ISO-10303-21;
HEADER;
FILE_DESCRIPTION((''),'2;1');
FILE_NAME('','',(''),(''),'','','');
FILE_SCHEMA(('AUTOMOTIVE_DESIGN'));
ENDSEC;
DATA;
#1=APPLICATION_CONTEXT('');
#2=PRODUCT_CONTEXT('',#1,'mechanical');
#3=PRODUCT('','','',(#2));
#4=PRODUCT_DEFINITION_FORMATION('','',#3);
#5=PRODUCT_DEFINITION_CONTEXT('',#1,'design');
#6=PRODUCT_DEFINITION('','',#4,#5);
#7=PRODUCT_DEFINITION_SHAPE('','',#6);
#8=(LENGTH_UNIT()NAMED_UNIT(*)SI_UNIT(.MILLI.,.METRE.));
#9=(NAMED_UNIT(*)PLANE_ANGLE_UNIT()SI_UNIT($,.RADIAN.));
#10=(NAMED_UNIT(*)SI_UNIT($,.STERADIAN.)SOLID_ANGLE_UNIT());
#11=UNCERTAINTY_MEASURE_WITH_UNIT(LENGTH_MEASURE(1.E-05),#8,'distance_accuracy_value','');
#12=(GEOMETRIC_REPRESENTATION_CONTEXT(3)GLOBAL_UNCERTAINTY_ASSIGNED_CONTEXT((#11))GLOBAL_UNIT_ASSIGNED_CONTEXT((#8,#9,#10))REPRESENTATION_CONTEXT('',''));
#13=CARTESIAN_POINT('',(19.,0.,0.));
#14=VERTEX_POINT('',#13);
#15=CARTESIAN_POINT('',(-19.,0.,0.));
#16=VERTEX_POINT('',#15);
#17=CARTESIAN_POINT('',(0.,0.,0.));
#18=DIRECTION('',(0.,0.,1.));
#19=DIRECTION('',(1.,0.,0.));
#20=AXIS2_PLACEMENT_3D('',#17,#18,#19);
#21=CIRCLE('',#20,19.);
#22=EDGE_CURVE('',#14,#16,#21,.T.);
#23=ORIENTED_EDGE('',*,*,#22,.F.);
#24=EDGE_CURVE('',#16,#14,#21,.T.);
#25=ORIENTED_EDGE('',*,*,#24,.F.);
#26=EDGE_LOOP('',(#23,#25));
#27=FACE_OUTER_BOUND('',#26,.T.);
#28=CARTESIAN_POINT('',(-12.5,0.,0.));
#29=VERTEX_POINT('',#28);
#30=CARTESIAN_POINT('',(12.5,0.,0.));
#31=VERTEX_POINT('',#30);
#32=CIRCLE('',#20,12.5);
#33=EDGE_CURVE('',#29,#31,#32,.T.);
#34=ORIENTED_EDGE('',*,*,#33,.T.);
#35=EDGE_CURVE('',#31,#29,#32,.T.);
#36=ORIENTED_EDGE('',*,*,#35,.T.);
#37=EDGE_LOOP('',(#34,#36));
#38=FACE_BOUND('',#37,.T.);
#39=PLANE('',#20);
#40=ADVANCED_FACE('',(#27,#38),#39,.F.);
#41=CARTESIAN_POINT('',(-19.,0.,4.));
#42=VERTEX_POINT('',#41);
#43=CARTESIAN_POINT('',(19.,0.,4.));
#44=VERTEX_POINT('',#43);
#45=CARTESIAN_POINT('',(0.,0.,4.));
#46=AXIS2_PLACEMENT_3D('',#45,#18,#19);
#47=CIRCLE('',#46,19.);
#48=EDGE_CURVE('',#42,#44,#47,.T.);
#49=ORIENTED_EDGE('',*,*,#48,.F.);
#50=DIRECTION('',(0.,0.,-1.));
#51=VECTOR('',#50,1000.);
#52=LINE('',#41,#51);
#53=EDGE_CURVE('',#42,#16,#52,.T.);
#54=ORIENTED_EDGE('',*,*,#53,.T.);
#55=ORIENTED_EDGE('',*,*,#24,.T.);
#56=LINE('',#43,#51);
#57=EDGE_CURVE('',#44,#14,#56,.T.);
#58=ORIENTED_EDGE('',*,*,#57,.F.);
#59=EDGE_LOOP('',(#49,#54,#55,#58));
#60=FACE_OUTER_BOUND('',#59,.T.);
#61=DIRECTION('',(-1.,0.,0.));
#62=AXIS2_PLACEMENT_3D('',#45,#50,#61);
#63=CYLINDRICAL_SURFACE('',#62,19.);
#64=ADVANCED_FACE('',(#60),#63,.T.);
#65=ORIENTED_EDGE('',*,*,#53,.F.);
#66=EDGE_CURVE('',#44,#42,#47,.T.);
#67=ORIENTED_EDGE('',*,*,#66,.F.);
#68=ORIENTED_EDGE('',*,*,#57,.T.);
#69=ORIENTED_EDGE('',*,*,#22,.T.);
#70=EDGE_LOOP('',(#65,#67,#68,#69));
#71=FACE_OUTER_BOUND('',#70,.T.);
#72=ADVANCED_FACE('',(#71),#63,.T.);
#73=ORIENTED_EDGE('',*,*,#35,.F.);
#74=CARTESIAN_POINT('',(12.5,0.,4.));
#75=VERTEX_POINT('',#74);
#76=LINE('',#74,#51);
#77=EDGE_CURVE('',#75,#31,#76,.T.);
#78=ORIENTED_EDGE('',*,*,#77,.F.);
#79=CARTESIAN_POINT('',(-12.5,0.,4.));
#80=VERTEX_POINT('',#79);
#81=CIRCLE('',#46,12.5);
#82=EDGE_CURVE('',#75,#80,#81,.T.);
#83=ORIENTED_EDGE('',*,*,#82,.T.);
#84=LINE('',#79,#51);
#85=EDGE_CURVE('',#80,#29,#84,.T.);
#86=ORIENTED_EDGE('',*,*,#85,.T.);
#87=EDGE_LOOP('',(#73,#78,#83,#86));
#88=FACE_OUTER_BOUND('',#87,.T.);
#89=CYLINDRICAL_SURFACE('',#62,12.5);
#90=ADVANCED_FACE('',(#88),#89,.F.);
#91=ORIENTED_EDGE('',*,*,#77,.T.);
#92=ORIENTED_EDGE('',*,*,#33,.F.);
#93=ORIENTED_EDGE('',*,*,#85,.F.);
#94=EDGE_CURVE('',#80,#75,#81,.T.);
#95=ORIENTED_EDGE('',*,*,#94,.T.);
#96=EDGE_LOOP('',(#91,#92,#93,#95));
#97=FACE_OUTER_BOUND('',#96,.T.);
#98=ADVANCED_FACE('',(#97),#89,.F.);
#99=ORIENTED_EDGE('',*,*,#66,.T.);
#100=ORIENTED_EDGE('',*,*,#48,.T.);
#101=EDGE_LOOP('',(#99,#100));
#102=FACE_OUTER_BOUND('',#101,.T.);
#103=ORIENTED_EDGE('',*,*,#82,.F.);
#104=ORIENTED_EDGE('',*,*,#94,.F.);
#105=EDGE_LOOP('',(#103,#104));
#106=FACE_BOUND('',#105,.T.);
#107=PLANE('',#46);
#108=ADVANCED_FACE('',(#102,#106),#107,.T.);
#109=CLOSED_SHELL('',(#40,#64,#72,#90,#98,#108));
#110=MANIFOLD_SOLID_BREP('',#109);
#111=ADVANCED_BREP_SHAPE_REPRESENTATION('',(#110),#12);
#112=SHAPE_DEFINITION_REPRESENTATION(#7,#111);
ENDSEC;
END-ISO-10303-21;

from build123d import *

# Parameters (mm, degrees)
SKETCH1_R      = 19
SKETCH1_R_2    = 12.5
EXTRUDE1_DEPTH = 4


with BuildPart() as part:
    # Sketch1 → Extrude1 (new body)
    with BuildSketch(Plane.XY):
        Circle(SKETCH1_R)
        Circle(SKETCH1_R_2, mode=Mode.SUBTRACT)
    extrude(amount=EXTRUDE1_DEPTH)


solid = part.part
